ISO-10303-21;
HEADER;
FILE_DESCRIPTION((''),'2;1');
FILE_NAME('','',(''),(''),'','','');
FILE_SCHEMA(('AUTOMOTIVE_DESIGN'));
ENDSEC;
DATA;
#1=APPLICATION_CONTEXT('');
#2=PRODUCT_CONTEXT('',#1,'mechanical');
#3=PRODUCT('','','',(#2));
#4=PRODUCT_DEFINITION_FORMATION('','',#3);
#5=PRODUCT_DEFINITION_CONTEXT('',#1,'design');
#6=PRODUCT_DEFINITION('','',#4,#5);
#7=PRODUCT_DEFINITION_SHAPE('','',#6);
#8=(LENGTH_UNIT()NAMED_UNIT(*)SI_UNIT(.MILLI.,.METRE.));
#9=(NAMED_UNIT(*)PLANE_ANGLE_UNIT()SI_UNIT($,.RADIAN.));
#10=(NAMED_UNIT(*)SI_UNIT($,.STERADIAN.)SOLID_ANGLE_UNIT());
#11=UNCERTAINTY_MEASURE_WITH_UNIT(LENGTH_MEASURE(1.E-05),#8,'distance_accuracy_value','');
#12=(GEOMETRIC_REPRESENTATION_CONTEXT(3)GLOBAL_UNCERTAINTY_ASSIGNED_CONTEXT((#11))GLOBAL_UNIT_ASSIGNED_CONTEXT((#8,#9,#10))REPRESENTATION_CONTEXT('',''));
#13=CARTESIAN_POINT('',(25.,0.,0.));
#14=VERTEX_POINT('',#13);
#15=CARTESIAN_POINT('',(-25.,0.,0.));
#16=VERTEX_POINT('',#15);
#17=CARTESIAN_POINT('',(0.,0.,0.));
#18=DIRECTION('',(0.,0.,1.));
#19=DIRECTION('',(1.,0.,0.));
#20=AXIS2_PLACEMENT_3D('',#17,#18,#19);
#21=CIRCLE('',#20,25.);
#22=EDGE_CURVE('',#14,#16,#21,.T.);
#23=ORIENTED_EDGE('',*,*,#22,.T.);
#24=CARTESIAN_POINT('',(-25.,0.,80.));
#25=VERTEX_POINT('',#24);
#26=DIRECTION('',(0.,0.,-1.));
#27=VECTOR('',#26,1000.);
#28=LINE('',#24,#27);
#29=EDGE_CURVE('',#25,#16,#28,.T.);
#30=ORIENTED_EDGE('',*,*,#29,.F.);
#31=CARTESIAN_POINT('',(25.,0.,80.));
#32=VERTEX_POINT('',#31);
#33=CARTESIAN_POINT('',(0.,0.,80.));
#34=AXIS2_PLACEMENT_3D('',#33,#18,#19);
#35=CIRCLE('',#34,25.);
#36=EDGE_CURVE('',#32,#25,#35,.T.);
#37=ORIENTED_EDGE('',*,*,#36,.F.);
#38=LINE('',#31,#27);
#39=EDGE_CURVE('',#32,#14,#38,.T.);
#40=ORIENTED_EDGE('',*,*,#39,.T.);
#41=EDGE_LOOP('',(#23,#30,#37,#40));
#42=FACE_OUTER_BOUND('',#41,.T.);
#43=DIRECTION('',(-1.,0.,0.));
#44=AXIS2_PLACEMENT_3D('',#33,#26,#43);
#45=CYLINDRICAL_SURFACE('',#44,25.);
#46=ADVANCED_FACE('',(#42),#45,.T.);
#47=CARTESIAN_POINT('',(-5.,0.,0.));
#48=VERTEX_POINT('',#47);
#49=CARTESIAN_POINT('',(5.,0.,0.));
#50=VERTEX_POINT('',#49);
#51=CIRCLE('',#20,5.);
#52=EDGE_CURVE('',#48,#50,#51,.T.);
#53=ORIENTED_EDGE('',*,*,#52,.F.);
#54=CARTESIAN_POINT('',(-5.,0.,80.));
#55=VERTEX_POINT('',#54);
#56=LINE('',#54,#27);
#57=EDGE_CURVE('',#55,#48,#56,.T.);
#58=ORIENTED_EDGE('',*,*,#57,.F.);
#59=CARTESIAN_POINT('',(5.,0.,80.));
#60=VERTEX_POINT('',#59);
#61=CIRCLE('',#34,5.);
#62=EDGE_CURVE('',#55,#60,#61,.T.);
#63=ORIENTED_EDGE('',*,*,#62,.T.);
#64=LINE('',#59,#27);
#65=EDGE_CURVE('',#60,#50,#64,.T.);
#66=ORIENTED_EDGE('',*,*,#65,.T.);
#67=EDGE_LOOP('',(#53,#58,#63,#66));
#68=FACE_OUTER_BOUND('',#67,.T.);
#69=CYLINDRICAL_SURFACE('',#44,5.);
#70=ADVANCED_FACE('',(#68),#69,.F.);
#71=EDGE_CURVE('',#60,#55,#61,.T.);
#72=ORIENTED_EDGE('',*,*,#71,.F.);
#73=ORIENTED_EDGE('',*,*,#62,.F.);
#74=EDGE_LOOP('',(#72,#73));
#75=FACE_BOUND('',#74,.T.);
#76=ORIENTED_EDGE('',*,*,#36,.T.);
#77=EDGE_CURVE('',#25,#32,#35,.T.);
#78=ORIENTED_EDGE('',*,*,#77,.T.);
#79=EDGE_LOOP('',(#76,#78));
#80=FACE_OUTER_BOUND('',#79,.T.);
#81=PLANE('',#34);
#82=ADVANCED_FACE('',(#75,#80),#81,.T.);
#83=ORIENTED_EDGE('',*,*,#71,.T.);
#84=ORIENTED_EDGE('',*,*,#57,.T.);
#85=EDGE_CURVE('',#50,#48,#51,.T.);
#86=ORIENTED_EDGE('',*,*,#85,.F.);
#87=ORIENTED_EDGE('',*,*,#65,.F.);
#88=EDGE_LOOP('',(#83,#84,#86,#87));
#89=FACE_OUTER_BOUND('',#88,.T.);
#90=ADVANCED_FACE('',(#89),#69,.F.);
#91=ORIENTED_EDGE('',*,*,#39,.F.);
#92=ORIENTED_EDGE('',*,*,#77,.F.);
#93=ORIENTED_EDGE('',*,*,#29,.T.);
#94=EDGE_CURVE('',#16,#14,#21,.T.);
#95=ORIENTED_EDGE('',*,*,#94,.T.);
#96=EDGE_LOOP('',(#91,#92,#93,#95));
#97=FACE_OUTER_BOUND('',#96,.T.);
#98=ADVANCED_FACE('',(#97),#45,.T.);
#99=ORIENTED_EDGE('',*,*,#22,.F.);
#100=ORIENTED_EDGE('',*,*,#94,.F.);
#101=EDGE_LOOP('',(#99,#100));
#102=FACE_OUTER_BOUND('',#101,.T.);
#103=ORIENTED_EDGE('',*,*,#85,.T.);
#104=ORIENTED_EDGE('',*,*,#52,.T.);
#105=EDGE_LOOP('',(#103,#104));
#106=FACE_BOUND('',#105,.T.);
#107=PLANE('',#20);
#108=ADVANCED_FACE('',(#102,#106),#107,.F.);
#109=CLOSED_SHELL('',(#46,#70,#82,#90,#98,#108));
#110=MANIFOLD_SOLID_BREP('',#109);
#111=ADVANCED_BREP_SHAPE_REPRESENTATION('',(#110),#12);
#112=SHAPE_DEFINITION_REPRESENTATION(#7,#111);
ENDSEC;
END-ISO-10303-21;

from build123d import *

# Parameters (mm, degrees)
SKETCH1_R           = 25
SKETCH1_R_2         = 5
BOSS_EXTRUDE1_DEPTH = 80


with BuildPart() as part:
    # Sketch1 → Boss-Extrude1 (new body)
    with BuildSketch(Plane.XY):
        Circle(SKETCH1_R)
        Circle(SKETCH1_R_2, mode=Mode.SUBTRACT)
    extrude(amount=BOSS_EXTRUDE1_DEPTH)


solid = part.part
